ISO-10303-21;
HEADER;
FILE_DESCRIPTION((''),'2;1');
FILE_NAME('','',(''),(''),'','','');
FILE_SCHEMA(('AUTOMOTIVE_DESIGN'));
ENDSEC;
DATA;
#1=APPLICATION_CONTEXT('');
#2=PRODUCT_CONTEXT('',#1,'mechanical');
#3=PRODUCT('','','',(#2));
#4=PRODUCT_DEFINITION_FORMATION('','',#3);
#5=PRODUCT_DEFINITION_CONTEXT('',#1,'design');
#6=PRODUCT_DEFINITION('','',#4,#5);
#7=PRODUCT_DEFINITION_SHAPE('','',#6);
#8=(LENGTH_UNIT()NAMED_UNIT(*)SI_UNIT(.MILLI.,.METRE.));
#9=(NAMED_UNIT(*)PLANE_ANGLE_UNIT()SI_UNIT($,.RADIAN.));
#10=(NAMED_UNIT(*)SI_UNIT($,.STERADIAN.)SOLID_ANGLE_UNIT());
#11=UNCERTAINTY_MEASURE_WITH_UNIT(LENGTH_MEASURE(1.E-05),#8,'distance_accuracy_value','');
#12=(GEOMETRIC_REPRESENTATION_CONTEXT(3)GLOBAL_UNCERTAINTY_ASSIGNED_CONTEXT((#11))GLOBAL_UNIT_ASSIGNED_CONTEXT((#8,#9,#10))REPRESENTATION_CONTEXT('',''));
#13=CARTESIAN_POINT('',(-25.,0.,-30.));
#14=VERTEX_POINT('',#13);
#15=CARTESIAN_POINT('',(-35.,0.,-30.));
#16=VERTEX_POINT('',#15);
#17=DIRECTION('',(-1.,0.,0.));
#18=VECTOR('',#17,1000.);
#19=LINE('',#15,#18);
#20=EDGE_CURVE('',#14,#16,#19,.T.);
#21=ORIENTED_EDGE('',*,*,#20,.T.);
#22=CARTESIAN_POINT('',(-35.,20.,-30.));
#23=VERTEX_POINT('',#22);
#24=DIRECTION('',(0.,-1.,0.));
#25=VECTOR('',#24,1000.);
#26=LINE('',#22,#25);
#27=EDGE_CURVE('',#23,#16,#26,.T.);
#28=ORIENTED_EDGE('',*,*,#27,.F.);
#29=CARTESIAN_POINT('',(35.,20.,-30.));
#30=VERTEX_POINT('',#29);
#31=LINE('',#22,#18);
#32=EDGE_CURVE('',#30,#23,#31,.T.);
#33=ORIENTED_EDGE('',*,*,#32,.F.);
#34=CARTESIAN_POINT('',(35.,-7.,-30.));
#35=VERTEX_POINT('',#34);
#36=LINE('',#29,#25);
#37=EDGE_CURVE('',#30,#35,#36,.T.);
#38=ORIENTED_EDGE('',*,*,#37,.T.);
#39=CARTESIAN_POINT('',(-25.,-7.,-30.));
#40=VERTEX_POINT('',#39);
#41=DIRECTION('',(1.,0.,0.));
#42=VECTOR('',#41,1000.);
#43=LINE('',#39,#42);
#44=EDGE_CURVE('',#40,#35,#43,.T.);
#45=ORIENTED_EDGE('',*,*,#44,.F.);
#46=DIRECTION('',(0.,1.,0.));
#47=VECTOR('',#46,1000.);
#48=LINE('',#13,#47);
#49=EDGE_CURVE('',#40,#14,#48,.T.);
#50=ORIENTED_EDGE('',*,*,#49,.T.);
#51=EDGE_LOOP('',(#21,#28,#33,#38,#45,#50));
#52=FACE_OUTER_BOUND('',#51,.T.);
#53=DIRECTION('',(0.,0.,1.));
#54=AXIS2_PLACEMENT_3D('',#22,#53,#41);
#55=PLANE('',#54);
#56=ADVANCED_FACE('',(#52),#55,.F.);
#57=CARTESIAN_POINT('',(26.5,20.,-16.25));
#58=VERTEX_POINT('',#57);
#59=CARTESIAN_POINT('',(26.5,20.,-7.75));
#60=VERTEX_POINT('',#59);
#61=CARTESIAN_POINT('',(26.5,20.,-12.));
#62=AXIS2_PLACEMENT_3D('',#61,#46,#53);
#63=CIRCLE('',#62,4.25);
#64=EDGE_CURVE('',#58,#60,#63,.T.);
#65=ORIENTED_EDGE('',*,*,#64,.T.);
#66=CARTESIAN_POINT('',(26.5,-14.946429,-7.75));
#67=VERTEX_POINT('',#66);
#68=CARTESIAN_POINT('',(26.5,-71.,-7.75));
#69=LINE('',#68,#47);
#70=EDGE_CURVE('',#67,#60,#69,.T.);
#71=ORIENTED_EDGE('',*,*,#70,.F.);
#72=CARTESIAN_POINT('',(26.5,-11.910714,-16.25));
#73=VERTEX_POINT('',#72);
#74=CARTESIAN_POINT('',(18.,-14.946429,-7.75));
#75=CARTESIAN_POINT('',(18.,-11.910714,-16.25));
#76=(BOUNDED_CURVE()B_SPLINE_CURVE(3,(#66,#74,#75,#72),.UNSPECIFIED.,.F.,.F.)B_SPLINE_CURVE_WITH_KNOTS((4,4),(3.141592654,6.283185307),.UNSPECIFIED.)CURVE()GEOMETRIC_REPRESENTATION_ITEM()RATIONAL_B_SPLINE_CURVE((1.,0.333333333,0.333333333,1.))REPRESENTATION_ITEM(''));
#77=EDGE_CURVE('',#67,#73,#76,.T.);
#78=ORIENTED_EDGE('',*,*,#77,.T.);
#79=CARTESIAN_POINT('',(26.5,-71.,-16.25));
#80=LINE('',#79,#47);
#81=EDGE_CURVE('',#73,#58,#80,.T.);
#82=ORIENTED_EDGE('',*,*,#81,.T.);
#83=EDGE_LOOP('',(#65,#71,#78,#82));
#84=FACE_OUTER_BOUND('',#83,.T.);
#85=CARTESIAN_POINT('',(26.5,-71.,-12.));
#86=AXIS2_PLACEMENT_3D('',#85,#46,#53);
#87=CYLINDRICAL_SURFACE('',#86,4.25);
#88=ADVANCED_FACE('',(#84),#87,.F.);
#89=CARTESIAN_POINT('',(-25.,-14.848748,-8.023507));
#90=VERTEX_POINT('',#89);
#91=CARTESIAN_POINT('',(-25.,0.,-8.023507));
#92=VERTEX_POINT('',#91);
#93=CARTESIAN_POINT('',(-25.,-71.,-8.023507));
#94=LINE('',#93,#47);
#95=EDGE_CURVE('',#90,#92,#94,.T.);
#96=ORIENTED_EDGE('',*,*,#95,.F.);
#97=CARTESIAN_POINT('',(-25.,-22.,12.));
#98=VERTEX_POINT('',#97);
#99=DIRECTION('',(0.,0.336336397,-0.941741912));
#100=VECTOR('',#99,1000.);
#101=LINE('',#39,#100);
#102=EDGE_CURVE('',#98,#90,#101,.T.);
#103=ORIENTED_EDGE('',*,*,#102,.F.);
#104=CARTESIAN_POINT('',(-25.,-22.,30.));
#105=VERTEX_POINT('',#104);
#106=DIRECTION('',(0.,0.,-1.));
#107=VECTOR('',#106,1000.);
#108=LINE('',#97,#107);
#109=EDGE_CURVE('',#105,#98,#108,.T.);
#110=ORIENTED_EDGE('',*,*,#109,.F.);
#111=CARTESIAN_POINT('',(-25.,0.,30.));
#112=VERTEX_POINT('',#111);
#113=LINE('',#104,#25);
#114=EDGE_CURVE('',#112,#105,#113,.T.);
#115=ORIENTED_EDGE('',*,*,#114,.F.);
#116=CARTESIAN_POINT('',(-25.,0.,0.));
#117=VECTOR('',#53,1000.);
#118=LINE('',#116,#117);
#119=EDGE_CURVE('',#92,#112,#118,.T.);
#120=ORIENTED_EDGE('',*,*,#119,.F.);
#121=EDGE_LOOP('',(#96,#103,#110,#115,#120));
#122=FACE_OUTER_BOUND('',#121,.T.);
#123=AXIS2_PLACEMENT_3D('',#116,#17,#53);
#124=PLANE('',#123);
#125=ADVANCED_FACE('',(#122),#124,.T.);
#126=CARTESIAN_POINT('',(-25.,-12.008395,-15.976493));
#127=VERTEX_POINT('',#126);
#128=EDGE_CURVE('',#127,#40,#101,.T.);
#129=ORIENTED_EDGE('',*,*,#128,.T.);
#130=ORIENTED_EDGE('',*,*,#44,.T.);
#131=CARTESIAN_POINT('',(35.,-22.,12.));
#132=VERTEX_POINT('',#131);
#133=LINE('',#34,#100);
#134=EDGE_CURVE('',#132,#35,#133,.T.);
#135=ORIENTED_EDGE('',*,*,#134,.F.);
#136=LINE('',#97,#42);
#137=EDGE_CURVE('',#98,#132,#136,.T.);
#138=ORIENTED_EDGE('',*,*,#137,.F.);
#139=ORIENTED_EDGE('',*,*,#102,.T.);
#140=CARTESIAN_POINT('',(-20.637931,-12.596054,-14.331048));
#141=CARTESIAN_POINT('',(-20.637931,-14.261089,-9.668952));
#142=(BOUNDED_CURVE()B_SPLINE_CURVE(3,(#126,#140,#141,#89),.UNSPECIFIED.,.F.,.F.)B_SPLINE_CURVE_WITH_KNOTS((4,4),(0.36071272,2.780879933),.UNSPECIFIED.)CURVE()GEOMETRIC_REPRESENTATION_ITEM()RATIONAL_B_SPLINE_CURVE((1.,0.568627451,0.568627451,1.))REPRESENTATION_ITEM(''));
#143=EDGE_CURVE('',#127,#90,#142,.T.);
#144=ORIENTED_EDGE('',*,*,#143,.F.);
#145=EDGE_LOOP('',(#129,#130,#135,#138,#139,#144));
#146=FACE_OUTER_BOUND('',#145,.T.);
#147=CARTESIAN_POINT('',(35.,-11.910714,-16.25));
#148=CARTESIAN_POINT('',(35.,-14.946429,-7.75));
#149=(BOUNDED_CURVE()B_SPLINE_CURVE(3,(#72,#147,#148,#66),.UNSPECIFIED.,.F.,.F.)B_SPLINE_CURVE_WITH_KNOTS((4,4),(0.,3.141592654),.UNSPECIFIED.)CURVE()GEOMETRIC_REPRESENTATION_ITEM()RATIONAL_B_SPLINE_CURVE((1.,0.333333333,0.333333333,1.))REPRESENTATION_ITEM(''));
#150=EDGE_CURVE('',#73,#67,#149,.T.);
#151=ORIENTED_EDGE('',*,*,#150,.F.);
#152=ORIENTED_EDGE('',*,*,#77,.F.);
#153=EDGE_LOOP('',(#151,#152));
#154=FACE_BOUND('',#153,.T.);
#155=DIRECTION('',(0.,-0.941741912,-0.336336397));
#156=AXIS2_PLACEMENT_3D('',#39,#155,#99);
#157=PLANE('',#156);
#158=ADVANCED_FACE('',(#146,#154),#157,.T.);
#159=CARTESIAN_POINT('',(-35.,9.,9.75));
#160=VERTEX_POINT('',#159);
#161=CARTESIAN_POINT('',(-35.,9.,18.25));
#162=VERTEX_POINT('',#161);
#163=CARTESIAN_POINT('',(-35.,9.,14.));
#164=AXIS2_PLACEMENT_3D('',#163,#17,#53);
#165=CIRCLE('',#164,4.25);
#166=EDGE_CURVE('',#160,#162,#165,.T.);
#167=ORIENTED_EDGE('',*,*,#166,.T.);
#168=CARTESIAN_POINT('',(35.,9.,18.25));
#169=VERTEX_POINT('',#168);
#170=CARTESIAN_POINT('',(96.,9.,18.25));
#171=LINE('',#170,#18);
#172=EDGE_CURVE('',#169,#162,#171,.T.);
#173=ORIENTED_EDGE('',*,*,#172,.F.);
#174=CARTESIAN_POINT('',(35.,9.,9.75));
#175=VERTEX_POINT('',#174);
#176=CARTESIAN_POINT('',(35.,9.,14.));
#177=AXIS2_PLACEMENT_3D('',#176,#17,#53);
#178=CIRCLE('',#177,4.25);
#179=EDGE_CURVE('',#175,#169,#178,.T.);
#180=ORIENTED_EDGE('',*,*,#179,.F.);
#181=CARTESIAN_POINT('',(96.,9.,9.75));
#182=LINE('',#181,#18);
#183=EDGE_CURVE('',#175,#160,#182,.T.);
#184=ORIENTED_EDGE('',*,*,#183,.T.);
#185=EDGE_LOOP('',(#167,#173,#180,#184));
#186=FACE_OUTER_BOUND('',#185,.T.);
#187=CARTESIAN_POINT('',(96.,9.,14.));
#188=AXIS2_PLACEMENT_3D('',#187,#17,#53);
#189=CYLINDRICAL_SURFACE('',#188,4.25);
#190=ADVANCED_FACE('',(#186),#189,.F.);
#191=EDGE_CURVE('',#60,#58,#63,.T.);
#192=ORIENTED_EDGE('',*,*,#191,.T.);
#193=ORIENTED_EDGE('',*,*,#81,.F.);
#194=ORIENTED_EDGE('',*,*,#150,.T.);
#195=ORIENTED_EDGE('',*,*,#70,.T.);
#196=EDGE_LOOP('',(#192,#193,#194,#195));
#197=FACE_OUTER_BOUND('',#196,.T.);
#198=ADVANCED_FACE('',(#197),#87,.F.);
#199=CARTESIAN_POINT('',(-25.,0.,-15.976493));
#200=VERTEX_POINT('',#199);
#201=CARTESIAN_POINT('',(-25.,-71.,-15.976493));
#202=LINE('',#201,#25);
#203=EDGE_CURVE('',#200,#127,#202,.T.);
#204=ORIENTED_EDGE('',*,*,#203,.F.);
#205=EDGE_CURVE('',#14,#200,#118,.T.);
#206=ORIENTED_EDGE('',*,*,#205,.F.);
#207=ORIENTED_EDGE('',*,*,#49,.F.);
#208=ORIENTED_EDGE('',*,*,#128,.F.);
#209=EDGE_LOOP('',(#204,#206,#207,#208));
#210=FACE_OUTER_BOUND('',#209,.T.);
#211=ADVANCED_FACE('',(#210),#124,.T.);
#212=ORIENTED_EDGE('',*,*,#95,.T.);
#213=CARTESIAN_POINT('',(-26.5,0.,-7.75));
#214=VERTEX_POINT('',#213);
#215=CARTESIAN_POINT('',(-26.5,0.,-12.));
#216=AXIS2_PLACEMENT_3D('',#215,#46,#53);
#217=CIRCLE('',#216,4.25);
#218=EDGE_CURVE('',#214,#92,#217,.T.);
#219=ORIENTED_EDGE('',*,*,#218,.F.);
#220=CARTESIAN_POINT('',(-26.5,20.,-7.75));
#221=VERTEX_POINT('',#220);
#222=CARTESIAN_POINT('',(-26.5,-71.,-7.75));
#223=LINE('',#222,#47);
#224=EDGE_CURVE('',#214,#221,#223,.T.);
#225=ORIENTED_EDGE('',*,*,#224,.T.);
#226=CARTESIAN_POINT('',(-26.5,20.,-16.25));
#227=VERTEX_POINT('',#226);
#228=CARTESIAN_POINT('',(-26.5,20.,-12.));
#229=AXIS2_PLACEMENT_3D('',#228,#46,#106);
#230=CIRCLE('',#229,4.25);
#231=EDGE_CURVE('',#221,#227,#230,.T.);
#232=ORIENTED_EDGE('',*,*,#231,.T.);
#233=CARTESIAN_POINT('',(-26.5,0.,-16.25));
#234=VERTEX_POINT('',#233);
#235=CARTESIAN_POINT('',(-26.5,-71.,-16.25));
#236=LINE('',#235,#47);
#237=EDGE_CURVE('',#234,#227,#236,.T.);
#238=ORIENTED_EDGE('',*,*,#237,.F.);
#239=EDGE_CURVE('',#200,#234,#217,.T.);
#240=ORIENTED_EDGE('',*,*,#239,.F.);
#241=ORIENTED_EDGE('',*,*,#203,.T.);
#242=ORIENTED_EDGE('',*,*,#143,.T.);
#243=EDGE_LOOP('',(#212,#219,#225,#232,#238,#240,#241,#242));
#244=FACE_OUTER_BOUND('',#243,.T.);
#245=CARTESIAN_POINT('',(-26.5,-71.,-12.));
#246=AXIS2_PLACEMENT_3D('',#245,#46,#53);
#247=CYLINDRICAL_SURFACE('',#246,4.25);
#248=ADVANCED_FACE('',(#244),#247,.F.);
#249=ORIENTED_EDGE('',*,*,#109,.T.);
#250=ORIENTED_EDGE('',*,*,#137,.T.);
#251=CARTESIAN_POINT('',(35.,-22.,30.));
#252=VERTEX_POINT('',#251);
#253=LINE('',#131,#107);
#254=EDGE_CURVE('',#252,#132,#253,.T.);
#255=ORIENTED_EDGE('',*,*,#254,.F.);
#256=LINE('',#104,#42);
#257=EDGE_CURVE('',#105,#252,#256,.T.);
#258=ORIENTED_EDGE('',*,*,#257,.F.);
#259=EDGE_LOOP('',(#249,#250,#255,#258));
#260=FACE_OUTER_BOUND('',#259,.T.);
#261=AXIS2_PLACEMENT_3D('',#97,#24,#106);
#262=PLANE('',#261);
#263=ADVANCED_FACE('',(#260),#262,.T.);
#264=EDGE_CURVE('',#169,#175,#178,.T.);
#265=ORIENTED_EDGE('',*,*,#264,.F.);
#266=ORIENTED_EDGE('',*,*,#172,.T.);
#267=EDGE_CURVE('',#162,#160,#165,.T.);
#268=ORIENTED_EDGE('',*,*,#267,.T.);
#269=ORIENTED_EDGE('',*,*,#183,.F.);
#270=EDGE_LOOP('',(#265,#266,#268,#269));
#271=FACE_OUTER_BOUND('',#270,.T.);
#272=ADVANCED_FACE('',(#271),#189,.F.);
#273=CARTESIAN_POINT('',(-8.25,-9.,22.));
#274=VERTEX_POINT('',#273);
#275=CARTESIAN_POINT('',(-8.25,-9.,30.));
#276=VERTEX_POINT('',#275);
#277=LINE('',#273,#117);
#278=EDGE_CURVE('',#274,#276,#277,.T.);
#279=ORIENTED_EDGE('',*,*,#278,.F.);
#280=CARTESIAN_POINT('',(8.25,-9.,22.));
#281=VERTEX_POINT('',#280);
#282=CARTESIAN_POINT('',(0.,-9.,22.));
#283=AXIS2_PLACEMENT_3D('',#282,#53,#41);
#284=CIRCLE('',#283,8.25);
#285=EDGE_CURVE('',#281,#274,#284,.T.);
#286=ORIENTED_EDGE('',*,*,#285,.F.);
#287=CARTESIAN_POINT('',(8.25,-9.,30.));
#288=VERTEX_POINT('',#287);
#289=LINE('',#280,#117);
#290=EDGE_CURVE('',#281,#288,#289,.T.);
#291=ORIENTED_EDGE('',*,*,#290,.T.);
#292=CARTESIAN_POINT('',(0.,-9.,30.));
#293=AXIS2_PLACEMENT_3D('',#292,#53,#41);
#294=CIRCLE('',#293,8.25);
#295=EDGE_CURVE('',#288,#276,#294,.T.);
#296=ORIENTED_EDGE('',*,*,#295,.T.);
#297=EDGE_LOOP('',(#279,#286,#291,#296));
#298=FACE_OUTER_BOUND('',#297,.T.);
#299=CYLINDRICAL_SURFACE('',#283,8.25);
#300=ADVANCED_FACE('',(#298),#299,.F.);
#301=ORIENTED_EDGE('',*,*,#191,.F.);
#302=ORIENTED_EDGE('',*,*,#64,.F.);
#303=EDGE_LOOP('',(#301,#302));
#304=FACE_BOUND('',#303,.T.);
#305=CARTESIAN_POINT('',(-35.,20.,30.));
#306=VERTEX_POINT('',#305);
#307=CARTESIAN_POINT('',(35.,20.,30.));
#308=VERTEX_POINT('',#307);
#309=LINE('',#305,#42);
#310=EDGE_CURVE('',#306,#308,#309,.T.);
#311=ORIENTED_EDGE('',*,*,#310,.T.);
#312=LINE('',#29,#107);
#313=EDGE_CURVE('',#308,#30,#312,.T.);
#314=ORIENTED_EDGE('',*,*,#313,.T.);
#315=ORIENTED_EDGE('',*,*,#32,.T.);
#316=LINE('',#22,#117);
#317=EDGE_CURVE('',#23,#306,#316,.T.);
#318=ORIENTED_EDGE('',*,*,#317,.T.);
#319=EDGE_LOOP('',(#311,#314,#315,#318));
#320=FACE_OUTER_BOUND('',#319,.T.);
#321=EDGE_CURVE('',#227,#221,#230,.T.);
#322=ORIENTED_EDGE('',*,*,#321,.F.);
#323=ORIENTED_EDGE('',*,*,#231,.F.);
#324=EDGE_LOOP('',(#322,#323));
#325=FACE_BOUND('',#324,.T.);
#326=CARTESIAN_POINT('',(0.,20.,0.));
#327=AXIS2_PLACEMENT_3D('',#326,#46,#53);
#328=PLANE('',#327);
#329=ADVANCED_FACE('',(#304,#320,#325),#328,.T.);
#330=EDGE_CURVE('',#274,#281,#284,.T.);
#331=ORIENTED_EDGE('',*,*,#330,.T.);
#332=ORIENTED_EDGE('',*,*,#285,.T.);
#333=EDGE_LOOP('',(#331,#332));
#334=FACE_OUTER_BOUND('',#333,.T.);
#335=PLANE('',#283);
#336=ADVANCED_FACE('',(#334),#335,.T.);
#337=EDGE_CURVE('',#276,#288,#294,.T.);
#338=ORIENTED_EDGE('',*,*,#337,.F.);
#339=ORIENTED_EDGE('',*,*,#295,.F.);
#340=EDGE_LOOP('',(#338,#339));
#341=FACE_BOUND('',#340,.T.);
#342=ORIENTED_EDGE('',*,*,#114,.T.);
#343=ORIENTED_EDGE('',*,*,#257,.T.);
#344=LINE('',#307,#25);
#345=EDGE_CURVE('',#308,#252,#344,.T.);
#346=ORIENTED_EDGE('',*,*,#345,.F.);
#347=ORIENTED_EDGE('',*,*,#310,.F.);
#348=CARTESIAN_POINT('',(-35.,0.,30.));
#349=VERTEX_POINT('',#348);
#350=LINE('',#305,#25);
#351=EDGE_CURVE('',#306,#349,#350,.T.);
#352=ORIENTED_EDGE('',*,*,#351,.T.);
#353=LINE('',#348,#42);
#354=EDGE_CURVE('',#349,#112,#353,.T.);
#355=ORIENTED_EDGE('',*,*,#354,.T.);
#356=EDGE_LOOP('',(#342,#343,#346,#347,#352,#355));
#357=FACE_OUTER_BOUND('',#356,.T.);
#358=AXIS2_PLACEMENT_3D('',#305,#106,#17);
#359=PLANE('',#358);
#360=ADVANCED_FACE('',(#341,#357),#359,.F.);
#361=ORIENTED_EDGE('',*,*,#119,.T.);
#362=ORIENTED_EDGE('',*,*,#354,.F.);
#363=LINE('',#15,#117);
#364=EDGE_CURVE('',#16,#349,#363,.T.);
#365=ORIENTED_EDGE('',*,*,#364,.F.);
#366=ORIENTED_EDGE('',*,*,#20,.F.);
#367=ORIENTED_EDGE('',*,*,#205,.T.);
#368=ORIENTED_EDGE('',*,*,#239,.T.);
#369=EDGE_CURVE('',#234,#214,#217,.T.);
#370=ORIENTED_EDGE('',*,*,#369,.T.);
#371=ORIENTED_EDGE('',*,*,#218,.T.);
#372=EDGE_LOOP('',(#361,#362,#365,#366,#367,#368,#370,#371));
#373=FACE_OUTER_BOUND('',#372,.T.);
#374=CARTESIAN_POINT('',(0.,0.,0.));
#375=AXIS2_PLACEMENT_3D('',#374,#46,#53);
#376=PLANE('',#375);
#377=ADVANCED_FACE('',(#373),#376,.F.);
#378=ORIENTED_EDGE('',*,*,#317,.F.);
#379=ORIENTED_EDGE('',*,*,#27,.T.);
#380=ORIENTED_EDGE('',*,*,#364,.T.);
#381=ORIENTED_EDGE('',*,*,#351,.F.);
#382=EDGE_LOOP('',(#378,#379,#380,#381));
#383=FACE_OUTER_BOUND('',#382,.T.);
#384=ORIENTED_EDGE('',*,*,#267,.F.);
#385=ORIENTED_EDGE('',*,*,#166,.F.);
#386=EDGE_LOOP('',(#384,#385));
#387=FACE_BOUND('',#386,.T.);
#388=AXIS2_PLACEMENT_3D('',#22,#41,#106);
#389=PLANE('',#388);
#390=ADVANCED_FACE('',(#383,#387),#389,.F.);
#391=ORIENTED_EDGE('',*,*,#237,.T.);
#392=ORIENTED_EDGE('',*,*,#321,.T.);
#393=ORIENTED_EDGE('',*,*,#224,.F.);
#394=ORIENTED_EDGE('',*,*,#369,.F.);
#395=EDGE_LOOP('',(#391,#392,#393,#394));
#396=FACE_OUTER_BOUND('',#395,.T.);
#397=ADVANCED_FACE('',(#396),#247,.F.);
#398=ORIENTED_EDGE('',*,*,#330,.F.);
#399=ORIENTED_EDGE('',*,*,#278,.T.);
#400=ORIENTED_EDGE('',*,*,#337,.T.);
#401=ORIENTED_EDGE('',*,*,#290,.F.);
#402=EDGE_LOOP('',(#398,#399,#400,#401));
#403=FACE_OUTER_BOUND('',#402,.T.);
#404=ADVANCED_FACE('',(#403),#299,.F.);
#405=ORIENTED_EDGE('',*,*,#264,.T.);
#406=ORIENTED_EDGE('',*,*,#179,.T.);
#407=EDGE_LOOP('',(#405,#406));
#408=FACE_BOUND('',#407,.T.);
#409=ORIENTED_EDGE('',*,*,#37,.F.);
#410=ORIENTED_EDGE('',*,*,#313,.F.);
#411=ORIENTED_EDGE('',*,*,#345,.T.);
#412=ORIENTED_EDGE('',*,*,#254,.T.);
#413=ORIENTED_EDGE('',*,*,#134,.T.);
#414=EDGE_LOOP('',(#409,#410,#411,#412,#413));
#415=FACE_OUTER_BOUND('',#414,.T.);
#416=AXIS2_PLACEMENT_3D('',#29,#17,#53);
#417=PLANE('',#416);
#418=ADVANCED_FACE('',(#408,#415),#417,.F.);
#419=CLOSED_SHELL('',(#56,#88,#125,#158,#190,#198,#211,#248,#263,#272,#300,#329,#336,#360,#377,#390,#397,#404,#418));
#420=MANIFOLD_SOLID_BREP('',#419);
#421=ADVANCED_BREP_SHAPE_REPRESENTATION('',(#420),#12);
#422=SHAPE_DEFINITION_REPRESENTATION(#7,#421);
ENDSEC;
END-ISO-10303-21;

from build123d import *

# Parameters (mm, degrees)
SKETCH1_W           = 70
SKETCH1_H           = 60
BOSS_EXTRUDE1_DEPTH = 20
BOSS_EXTRUDE2_DEPTH = 60
SKETCH5_R           = 4.25
CUT_EXTRUDE3_DEPTH  = 131
SKETCH7_R           = 4.25
CUT_EXTRUDE4_DEPTH  = 91
SKETCH8_R           = 8.25
CUT_EXTRUDE5_DEPTH  = 8


with BuildPart() as part:
    # Sketch1 → Boss-Extrude1 (new body)
    with BuildSketch(Plane(origin=(0, 0, 0), x_dir=(1, 0, 0), z_dir=(0, 1, 0))):
        Rectangle(SKETCH1_W, SKETCH1_H)
    extrude(amount=BOSS_EXTRUDE1_DEPTH)

    # Sketch2 → Boss-Extrude2 (add)
    with BuildSketch(Plane(origin=(35, 0, 0), x_dir=(0, 0, -1), z_dir=(1, 0, 0))):
        Polygon((30, 20), (30, 0), (30, -7), (-12, -22), (-30, -22), (-30, 20), align=None)
    extrude(amount=-BOSS_EXTRUDE2_DEPTH)

    # Sketch5 → Cut-Extrude3 (cut)
    with BuildSketch(Plane.ZY.offset(35)):
        with Locations((14, 9)):
            Circle(SKETCH5_R)
    extrude(amount=-CUT_EXTRUDE3_DEPTH, mode=Mode.SUBTRACT)

    # Sketch7 → Cut-Extrude4 (cut)
    with BuildSketch(Plane(origin=(0, 20, 0), x_dir=(1, 0, 0), z_dir=(0, 1, 0))):
        with Locations(Location((26.5, 12, 0), (0, 0, 270))):
            Circle(SKETCH7_R)
        with Locations(Location((-26.5, 12, 0), (0, 0, 290.667316494))):
            Circle(SKETCH7_R)
    extrude(amount=-CUT_EXTRUDE4_DEPTH, mode=Mode.SUBTRACT)

    # Sketch8 → Cut-Extrude5 (cut)
    with BuildSketch(Plane.XY.offset(30)):
        with Locations((0, -9)):
            Circle(SKETCH8_R)
    extrude(amount=-CUT_EXTRUDE5_DEPTH, mode=Mode.SUBTRACT)


solid = part.part
